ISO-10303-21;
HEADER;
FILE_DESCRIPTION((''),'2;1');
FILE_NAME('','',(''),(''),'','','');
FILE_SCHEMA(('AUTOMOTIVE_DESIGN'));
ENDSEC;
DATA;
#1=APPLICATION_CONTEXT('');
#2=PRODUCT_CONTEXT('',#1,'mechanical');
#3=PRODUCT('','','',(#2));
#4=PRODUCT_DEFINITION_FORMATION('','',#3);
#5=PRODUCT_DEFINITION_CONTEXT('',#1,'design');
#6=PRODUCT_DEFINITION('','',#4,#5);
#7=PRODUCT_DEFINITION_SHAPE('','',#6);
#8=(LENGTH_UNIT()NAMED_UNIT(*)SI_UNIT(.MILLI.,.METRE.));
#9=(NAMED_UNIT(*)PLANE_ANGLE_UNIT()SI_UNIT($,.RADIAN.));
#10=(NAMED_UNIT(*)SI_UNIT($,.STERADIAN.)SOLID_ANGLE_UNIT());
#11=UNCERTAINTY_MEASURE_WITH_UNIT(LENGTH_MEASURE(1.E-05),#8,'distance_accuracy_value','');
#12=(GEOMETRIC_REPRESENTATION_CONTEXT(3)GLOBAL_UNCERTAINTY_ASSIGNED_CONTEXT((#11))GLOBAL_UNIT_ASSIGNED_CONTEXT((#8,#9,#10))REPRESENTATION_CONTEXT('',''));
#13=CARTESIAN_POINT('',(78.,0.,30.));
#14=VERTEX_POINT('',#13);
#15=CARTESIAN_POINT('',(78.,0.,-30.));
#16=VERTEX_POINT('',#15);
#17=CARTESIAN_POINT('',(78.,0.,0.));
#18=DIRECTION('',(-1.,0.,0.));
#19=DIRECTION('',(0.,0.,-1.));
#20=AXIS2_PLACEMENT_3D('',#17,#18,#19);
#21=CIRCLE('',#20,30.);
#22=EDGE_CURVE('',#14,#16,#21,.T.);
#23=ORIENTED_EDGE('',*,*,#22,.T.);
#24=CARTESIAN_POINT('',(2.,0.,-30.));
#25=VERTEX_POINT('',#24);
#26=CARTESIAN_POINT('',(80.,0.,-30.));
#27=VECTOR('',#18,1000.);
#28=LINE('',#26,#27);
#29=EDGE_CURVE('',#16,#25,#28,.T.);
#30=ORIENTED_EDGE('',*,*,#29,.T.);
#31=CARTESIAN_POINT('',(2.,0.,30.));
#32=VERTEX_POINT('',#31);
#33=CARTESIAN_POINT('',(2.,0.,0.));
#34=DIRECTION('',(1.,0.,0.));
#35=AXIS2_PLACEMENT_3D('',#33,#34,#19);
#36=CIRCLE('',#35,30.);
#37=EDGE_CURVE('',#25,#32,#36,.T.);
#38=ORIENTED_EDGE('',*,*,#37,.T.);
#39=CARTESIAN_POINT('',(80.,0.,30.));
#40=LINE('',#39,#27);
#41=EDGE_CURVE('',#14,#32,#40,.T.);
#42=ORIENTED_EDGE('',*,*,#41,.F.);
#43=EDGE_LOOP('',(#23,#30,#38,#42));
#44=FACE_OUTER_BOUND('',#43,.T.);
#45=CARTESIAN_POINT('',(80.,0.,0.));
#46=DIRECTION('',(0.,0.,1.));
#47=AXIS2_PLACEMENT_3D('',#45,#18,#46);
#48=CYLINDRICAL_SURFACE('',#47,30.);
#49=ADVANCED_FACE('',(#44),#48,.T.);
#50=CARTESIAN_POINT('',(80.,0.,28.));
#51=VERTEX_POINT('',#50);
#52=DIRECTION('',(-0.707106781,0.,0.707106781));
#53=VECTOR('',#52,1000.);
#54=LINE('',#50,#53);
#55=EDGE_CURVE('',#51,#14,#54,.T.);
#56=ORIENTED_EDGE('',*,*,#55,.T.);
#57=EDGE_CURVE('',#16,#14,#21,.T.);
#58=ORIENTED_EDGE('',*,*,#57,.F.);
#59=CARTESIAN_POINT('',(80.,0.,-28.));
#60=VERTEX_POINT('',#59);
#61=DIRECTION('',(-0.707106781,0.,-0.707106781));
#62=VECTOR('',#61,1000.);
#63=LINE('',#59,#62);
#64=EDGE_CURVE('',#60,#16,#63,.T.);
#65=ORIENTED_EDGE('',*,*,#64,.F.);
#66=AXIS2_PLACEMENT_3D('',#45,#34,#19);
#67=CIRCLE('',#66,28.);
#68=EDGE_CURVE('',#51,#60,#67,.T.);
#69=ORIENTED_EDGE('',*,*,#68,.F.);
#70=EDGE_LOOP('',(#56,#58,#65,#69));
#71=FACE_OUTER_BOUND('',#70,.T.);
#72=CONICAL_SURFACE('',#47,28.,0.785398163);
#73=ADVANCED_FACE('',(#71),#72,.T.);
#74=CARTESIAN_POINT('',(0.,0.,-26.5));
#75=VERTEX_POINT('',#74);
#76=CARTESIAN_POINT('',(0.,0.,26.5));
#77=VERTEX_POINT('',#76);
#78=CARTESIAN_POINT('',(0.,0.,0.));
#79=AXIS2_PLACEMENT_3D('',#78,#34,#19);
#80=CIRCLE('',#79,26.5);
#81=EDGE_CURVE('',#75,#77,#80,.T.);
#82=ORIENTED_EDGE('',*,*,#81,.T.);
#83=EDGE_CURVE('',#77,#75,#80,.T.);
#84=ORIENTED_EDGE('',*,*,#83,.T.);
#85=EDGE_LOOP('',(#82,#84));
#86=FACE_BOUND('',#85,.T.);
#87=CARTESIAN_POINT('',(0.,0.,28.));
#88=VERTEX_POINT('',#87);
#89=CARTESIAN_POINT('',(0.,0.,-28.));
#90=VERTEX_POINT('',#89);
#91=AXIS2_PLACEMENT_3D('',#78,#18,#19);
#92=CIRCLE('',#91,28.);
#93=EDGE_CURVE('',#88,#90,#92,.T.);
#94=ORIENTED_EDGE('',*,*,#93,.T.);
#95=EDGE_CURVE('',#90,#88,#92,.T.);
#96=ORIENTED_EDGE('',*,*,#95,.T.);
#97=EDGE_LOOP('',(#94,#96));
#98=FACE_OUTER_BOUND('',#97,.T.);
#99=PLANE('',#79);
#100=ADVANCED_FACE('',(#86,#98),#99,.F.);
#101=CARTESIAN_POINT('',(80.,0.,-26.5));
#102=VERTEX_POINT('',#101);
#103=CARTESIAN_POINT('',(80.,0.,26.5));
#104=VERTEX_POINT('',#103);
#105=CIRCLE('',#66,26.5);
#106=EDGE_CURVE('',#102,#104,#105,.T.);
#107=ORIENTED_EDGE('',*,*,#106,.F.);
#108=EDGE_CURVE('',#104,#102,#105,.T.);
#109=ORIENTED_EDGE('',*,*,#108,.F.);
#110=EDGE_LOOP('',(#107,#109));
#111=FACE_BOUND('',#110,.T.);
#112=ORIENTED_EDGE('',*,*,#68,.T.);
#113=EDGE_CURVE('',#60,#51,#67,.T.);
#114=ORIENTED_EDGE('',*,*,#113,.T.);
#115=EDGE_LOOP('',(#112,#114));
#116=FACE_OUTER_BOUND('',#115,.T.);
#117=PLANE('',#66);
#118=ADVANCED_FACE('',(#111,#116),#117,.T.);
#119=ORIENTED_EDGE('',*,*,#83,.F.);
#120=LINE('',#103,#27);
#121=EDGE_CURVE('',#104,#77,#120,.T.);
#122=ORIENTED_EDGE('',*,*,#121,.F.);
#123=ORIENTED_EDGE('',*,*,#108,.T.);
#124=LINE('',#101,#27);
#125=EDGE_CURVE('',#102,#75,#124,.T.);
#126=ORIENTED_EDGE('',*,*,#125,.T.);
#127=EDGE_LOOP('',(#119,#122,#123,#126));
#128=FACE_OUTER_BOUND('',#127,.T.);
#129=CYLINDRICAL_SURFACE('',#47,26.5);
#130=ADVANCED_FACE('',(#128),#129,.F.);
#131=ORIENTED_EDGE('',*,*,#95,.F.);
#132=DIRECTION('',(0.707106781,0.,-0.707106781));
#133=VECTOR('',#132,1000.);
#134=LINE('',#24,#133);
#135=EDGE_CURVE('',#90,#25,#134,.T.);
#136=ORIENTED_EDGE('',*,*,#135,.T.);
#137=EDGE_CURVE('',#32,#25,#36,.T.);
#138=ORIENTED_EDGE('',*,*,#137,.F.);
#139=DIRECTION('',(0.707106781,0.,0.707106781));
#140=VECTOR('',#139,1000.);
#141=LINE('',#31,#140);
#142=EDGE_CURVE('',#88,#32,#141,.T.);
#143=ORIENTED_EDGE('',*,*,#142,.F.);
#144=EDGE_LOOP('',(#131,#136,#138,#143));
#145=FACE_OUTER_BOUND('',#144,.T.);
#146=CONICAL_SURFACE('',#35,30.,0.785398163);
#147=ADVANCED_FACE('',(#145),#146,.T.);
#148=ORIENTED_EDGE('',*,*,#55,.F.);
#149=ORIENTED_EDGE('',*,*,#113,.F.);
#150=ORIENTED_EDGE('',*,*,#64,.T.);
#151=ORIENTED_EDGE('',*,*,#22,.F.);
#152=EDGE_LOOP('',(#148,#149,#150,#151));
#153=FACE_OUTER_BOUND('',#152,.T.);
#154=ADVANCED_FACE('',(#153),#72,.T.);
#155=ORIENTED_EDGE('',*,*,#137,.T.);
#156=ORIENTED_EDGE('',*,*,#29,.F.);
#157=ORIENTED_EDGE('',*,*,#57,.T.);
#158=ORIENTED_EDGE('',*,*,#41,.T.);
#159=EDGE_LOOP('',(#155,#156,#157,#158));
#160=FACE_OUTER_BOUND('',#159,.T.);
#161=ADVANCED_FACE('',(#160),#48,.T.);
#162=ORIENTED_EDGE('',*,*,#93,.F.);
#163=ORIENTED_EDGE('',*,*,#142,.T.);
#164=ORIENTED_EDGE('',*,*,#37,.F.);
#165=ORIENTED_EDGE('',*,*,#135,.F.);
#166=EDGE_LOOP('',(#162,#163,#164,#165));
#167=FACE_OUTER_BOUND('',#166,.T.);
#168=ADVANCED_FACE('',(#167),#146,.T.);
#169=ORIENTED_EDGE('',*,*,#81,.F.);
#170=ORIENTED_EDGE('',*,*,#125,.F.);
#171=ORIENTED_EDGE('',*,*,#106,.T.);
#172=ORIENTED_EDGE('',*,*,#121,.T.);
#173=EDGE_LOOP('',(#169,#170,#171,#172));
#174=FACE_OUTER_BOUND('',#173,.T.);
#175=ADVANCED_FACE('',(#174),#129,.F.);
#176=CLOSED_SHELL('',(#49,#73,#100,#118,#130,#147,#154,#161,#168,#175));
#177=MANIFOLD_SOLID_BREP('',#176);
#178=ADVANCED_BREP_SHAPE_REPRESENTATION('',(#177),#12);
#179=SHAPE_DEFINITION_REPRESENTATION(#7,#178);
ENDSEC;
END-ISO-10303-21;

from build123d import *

# Parameters (mm, degrees)
SKETCH_1_R      = 30
SKETCH_1_R_2    = 26.5
EXTRUDE_1_DEPTH = 80
CHAMFER_1_SIZE  = 2


with BuildPart() as part:
    # 草图1 → 拉伸-薄壁1 (new body)
    with BuildSketch(Plane(origin=(0, 0, 0), x_dir=(0, 0, -1), z_dir=(1, 0, 0))):
        Circle(SKETCH_1_R)
        Circle(SKETCH_1_R_2, mode=Mode.SUBTRACT)
    extrude(amount=EXTRUDE_1_DEPTH)

    # 倒角1
    chamfer_1_edges = [part.edges().sort_by_distance(p)[0] for p in [
        (0, 0, 30),
        (80, 0, 30),
    ]]
    chamfer(chamfer_1_edges, length=CHAMFER_1_SIZE)


solid = part.part
